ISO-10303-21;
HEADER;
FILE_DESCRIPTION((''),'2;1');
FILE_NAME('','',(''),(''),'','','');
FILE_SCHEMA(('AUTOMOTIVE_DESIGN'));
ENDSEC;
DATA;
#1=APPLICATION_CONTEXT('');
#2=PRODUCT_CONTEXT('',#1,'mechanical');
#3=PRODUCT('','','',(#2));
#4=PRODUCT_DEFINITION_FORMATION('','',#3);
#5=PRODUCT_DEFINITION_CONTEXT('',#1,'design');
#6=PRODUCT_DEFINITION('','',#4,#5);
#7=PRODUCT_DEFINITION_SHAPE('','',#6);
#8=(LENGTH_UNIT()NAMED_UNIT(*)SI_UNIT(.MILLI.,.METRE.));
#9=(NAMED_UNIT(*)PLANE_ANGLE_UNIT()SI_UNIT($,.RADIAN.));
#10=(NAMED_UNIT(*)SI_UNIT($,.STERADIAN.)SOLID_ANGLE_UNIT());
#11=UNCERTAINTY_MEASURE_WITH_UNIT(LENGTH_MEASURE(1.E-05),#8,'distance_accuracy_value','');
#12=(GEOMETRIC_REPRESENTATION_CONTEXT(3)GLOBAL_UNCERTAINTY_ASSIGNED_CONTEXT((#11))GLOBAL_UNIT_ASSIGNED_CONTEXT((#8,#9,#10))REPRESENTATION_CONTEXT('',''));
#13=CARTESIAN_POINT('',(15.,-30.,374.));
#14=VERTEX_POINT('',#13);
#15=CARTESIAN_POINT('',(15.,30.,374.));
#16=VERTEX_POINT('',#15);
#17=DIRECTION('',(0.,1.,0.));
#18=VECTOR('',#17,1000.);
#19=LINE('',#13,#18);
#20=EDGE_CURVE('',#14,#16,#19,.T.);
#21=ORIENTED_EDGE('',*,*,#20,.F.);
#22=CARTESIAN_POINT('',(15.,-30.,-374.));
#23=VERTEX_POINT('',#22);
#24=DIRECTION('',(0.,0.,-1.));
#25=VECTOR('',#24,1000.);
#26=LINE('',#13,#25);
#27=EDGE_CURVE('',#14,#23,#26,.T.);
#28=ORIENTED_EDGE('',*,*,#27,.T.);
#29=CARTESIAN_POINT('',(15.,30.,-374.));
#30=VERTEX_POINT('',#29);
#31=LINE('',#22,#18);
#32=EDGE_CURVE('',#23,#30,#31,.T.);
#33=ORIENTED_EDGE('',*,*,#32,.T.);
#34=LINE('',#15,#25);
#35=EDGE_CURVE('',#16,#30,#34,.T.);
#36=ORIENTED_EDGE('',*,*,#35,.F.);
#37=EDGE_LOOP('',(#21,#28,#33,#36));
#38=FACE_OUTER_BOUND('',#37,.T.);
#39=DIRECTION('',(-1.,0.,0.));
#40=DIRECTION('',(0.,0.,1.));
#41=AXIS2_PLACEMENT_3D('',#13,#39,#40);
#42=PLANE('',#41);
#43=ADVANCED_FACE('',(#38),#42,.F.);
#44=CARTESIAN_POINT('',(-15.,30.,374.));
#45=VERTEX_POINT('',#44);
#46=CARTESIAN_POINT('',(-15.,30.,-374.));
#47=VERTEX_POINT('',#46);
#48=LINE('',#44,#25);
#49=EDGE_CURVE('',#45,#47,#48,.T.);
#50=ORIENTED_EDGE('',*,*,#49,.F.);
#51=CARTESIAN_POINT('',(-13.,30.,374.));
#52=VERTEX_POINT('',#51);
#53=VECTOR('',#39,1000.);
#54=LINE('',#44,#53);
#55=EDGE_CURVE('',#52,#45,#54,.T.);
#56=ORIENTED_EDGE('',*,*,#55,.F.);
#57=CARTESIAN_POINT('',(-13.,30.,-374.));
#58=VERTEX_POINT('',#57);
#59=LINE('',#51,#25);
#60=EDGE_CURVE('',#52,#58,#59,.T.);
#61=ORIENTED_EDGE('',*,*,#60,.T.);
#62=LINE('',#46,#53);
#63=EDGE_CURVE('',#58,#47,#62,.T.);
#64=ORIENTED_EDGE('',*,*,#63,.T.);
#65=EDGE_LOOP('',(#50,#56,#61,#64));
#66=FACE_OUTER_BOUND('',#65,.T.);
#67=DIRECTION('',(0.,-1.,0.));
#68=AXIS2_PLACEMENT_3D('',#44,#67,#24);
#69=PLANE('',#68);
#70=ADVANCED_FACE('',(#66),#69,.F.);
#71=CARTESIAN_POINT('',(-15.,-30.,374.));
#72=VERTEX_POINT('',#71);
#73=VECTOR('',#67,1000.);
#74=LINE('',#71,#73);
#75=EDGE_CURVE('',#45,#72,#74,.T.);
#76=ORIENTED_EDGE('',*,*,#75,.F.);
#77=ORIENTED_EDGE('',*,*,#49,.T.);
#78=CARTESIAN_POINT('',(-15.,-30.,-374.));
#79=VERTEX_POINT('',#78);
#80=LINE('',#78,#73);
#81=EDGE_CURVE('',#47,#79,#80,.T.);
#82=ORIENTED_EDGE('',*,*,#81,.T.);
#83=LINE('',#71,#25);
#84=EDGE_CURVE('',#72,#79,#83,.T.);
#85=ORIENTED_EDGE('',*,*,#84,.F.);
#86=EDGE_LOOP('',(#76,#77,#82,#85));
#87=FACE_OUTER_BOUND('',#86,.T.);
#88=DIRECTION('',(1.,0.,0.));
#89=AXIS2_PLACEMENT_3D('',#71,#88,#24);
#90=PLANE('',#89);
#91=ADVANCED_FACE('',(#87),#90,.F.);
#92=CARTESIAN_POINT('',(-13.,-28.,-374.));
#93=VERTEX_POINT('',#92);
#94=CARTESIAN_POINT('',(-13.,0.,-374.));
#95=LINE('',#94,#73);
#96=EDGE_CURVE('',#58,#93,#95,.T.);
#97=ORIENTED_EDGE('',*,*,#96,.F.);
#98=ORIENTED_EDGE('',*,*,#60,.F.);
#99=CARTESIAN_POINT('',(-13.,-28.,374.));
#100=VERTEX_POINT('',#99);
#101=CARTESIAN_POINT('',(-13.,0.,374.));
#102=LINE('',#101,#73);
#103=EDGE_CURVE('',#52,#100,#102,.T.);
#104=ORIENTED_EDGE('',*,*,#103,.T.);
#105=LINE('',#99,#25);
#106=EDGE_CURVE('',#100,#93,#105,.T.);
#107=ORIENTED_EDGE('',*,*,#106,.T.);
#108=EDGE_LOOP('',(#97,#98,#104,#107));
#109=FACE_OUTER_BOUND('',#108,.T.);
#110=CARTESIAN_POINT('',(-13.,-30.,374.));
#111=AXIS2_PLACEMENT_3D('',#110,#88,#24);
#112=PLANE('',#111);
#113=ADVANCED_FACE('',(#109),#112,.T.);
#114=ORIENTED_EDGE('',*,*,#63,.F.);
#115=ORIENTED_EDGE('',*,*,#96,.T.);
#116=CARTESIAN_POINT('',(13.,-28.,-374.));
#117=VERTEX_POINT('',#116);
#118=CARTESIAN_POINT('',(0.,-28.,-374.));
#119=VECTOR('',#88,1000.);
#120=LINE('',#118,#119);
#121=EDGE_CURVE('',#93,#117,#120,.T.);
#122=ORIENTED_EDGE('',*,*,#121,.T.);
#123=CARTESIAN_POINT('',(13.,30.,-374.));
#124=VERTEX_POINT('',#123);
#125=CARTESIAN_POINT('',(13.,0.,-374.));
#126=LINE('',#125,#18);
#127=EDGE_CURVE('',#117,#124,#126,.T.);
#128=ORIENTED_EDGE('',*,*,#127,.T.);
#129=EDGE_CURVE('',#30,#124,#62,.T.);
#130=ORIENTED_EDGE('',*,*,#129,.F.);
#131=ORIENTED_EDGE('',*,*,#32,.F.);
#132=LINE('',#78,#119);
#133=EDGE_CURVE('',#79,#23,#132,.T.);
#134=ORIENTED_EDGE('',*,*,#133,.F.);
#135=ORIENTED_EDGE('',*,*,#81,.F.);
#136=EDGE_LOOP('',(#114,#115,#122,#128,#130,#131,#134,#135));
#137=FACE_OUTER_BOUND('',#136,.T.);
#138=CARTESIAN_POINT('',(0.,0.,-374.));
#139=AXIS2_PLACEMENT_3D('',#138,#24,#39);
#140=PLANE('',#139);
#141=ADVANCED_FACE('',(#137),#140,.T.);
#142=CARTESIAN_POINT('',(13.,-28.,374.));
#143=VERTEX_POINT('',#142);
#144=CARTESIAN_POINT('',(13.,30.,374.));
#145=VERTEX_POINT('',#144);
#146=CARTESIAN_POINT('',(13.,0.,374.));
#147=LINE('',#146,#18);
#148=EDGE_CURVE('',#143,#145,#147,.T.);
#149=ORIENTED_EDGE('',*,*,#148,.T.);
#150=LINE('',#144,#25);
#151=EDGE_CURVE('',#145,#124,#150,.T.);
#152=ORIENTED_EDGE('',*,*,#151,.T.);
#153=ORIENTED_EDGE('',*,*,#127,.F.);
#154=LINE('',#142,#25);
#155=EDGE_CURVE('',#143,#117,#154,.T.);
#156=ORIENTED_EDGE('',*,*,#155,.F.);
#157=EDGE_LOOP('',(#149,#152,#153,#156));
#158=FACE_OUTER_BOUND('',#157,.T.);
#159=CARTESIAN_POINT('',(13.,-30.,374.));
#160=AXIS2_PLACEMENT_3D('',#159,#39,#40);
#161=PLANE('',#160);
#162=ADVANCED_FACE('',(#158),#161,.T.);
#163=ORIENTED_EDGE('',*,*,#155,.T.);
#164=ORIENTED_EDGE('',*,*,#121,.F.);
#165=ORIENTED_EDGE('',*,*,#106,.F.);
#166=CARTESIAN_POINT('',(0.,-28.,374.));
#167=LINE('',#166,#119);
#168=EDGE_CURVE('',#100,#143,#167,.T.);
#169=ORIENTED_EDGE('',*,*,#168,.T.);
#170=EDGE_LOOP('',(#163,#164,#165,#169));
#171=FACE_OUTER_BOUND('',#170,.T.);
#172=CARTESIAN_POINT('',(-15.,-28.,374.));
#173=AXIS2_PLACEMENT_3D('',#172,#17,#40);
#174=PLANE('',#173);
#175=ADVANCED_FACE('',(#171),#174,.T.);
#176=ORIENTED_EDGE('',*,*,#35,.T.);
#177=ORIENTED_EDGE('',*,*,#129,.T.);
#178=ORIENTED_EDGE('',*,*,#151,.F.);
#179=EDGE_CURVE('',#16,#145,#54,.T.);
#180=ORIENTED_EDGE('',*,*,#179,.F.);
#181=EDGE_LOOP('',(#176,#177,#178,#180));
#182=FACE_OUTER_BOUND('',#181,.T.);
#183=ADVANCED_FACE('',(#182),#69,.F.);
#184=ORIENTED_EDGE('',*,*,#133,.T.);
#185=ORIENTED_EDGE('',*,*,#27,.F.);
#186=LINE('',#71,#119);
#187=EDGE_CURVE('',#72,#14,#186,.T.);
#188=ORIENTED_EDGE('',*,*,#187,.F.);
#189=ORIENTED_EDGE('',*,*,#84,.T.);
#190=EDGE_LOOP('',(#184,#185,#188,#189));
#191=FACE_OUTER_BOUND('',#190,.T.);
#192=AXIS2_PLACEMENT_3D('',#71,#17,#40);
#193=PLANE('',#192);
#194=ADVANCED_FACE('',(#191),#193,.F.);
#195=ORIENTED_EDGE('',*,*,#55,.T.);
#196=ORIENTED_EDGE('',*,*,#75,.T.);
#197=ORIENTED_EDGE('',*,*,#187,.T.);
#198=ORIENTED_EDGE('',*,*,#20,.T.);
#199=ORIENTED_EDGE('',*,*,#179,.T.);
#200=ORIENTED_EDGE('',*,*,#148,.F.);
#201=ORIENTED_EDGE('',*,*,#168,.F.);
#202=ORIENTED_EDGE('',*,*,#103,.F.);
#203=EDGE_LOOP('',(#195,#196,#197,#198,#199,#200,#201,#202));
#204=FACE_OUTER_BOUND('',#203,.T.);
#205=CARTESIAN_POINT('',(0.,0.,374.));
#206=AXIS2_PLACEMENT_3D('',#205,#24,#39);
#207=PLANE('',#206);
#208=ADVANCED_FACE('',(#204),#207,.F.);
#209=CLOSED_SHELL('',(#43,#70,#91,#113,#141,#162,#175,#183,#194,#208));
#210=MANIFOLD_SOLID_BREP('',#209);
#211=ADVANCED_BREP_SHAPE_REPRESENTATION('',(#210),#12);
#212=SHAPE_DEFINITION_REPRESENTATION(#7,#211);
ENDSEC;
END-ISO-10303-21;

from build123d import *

# Parameters (mm, degrees)
SKETCH_1_W      = 30
SKETCH_1_H      = 60
EXTRUDE_1_DEPTH = 374
SHELL_1_T       = -2


with BuildPart() as part:
    # 草图1 → 凸台-拉伸1 (new, symmetric)
    with BuildSketch(Plane.XY):
        Rectangle(SKETCH_1_W, SKETCH_1_H)
    extrude(amount=EXTRUDE_1_DEPTH, both=True)

    # 抽壳1
    shell_1_openings = [part.faces().sort_by_distance(p)[0] for p in [
        (0, 0, 374),
        (0, 0, -374),
        (0, 30, 0),
    ]]
    offset(amount=SHELL_1_T, openings=shell_1_openings, kind=Kind.INTERSECTION)


solid = part.part
